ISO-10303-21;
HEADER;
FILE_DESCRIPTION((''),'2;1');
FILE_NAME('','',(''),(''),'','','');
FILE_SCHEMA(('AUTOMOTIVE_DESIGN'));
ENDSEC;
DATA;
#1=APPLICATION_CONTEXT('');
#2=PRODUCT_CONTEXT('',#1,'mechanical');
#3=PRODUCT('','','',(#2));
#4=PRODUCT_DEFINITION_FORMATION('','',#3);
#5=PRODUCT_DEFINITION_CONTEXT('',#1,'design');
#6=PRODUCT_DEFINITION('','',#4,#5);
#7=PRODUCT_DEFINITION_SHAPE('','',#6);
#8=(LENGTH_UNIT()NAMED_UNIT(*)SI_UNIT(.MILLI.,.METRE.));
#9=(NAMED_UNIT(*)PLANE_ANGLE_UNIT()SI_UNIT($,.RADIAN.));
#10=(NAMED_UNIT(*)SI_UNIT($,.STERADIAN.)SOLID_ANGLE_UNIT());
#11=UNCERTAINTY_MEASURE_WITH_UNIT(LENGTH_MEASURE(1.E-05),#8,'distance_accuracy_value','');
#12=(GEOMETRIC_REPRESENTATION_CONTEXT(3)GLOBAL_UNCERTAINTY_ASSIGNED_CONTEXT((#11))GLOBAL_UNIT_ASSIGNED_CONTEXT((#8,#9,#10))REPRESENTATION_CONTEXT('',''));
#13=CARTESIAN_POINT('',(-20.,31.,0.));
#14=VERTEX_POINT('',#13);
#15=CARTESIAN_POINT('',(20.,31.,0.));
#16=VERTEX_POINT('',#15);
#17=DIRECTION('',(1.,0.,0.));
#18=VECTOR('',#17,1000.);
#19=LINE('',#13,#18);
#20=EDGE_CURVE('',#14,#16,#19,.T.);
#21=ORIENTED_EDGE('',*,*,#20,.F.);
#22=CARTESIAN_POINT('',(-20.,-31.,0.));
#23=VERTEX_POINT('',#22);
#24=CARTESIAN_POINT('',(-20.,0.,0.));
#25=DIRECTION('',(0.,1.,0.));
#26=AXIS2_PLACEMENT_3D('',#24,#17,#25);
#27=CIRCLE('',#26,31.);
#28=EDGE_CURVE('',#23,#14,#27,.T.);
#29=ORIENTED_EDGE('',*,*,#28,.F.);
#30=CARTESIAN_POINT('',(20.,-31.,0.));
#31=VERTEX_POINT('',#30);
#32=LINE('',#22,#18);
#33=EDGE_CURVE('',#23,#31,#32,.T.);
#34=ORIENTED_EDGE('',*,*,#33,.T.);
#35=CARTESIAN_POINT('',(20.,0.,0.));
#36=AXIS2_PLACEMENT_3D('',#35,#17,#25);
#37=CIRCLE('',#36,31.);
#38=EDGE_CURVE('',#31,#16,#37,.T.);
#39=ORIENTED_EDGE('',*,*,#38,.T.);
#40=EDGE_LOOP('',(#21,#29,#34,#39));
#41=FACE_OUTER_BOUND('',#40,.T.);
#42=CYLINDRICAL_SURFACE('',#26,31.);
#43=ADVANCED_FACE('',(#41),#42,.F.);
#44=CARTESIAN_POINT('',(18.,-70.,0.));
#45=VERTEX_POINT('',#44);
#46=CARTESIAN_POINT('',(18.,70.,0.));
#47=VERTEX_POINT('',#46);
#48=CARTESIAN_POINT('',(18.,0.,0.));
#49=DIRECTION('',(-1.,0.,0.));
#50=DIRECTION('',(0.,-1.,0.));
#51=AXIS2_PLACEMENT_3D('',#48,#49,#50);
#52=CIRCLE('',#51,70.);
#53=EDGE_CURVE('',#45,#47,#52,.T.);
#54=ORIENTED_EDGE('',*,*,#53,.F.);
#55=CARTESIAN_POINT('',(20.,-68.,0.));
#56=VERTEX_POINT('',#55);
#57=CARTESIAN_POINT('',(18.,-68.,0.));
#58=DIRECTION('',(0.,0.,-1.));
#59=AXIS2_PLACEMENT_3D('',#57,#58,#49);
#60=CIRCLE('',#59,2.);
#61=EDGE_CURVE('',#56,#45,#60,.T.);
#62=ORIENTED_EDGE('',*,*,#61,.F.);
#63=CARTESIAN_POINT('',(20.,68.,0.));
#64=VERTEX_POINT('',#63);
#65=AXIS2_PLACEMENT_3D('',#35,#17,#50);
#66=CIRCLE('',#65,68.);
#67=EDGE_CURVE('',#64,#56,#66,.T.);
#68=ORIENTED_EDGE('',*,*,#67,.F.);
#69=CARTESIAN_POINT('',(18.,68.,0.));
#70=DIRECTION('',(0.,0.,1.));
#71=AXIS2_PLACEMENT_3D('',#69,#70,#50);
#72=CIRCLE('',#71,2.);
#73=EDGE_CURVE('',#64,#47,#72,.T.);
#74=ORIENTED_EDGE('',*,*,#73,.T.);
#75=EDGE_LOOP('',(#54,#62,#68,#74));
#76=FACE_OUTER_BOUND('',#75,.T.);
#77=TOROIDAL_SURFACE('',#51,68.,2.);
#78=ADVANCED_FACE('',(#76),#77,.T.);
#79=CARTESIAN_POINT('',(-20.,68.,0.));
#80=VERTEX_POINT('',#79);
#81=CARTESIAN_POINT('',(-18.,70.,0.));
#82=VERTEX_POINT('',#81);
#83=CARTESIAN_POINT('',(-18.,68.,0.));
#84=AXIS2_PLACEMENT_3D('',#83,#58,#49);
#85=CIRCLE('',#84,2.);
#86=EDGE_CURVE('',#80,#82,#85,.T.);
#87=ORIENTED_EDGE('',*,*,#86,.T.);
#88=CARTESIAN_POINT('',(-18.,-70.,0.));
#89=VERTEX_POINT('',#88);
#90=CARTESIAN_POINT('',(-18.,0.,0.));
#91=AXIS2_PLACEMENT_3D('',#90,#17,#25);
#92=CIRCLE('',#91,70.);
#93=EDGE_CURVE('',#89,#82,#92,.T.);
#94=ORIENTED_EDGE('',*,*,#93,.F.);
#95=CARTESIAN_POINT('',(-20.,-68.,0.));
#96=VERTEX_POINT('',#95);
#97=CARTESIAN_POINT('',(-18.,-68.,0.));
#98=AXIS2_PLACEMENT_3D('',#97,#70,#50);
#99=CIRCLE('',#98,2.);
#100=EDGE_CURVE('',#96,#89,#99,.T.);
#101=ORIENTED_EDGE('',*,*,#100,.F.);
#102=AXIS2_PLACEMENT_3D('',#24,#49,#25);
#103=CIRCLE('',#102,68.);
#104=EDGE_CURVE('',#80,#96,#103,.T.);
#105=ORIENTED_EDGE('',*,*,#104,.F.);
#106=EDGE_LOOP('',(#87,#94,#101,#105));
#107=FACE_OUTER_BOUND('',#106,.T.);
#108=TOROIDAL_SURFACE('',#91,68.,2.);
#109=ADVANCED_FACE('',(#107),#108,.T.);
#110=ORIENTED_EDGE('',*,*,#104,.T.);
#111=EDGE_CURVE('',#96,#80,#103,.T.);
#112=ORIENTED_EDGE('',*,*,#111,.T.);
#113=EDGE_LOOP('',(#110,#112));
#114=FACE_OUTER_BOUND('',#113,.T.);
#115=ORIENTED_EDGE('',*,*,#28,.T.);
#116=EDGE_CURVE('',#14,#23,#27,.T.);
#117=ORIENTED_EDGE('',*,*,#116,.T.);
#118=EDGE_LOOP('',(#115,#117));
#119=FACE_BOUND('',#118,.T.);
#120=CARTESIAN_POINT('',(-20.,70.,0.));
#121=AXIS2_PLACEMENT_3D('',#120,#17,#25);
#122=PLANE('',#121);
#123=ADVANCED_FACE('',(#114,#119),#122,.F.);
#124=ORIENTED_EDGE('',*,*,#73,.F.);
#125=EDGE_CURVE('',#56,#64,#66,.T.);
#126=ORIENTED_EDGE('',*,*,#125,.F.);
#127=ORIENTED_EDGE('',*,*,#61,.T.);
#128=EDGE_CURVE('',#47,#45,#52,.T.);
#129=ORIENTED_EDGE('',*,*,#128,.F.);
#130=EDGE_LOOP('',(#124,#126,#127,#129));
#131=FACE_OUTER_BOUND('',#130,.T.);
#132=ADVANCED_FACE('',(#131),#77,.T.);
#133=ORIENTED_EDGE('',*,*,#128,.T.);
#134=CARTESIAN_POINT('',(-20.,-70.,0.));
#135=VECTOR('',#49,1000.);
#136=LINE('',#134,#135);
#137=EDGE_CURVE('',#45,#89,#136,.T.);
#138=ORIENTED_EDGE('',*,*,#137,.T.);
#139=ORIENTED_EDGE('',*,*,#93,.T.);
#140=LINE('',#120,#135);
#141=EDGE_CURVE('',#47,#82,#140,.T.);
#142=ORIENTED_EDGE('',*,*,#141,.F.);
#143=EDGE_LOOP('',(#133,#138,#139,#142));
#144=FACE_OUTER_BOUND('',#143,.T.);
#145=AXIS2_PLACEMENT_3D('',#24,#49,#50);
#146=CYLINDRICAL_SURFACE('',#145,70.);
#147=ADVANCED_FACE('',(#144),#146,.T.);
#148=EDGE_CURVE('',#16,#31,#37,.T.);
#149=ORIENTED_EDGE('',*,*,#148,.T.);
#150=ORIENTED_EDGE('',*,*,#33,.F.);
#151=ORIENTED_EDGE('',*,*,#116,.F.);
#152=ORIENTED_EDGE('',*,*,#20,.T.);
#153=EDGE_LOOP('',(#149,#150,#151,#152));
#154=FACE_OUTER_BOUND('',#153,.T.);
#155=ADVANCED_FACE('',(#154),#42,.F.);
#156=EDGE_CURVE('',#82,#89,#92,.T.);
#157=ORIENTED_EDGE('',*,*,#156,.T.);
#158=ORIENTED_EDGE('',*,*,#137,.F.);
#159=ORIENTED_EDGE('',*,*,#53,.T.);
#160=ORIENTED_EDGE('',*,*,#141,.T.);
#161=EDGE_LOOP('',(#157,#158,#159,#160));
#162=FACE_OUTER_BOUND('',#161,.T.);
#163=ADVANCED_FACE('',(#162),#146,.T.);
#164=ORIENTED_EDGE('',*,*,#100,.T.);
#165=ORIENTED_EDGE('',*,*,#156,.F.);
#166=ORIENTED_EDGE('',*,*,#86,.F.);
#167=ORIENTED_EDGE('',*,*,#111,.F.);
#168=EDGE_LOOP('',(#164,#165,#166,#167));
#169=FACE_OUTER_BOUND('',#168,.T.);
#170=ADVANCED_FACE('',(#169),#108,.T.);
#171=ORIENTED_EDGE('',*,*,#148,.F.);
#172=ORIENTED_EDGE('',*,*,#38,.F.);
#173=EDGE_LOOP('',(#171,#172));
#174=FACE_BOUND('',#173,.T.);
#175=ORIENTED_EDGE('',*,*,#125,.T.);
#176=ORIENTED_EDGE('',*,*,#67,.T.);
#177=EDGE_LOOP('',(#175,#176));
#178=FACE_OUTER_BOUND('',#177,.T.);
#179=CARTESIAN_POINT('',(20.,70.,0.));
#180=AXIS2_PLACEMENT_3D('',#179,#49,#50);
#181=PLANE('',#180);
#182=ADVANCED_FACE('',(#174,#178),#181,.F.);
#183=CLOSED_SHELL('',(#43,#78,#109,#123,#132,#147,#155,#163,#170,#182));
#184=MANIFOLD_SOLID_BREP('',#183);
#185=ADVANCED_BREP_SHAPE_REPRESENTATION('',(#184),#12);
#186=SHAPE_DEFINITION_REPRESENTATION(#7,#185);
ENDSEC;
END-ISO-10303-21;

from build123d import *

# Parameters (mm, degrees)
SKETCH_1_W          = 40
SKETCH_1_H          = 70
SKETCH_2_R          = 31
CUT_EXTRUDE_1_DEPTH = 107.77078252
FILLET_1_R          = 2


with BuildPart() as part:
    # 草图1 → 旋转1 (revolve)
    with BuildSketch(Plane.XY, mode=Mode.PRIVATE) as revolve_1_sk:
        with Locations((0, 35)):
            Rectangle(SKETCH_1_W, SKETCH_1_H)
    revolve(revolve_1_sk.sketch.rotate(Axis((-20, 0, 0), (1, 0, 0)), 180), axis=Axis((-20, 0, 0), (1, 0, 0)))

    # 草图2 → 切除-拉伸1 (cut, through all)
    with BuildSketch(Plane(origin=(20, 0, 0), x_dir=(0, 0, -1), z_dir=(1, 0, 0))):
        with Locations(Location((0, 0, 0), (0, 0, 90))):
            Circle(SKETCH_2_R)
    extrude(amount=-CUT_EXTRUDE_1_DEPTH, mode=Mode.SUBTRACT)

    # 圆角1
    fillet_1_edges = [part.edges().sort_by_distance(p)[0] for p in [
        (-20, 70, 0),
        (20, 70, 0),
    ]]
    fillet(fillet_1_edges, radius=FILLET_1_R)


solid = part.part
